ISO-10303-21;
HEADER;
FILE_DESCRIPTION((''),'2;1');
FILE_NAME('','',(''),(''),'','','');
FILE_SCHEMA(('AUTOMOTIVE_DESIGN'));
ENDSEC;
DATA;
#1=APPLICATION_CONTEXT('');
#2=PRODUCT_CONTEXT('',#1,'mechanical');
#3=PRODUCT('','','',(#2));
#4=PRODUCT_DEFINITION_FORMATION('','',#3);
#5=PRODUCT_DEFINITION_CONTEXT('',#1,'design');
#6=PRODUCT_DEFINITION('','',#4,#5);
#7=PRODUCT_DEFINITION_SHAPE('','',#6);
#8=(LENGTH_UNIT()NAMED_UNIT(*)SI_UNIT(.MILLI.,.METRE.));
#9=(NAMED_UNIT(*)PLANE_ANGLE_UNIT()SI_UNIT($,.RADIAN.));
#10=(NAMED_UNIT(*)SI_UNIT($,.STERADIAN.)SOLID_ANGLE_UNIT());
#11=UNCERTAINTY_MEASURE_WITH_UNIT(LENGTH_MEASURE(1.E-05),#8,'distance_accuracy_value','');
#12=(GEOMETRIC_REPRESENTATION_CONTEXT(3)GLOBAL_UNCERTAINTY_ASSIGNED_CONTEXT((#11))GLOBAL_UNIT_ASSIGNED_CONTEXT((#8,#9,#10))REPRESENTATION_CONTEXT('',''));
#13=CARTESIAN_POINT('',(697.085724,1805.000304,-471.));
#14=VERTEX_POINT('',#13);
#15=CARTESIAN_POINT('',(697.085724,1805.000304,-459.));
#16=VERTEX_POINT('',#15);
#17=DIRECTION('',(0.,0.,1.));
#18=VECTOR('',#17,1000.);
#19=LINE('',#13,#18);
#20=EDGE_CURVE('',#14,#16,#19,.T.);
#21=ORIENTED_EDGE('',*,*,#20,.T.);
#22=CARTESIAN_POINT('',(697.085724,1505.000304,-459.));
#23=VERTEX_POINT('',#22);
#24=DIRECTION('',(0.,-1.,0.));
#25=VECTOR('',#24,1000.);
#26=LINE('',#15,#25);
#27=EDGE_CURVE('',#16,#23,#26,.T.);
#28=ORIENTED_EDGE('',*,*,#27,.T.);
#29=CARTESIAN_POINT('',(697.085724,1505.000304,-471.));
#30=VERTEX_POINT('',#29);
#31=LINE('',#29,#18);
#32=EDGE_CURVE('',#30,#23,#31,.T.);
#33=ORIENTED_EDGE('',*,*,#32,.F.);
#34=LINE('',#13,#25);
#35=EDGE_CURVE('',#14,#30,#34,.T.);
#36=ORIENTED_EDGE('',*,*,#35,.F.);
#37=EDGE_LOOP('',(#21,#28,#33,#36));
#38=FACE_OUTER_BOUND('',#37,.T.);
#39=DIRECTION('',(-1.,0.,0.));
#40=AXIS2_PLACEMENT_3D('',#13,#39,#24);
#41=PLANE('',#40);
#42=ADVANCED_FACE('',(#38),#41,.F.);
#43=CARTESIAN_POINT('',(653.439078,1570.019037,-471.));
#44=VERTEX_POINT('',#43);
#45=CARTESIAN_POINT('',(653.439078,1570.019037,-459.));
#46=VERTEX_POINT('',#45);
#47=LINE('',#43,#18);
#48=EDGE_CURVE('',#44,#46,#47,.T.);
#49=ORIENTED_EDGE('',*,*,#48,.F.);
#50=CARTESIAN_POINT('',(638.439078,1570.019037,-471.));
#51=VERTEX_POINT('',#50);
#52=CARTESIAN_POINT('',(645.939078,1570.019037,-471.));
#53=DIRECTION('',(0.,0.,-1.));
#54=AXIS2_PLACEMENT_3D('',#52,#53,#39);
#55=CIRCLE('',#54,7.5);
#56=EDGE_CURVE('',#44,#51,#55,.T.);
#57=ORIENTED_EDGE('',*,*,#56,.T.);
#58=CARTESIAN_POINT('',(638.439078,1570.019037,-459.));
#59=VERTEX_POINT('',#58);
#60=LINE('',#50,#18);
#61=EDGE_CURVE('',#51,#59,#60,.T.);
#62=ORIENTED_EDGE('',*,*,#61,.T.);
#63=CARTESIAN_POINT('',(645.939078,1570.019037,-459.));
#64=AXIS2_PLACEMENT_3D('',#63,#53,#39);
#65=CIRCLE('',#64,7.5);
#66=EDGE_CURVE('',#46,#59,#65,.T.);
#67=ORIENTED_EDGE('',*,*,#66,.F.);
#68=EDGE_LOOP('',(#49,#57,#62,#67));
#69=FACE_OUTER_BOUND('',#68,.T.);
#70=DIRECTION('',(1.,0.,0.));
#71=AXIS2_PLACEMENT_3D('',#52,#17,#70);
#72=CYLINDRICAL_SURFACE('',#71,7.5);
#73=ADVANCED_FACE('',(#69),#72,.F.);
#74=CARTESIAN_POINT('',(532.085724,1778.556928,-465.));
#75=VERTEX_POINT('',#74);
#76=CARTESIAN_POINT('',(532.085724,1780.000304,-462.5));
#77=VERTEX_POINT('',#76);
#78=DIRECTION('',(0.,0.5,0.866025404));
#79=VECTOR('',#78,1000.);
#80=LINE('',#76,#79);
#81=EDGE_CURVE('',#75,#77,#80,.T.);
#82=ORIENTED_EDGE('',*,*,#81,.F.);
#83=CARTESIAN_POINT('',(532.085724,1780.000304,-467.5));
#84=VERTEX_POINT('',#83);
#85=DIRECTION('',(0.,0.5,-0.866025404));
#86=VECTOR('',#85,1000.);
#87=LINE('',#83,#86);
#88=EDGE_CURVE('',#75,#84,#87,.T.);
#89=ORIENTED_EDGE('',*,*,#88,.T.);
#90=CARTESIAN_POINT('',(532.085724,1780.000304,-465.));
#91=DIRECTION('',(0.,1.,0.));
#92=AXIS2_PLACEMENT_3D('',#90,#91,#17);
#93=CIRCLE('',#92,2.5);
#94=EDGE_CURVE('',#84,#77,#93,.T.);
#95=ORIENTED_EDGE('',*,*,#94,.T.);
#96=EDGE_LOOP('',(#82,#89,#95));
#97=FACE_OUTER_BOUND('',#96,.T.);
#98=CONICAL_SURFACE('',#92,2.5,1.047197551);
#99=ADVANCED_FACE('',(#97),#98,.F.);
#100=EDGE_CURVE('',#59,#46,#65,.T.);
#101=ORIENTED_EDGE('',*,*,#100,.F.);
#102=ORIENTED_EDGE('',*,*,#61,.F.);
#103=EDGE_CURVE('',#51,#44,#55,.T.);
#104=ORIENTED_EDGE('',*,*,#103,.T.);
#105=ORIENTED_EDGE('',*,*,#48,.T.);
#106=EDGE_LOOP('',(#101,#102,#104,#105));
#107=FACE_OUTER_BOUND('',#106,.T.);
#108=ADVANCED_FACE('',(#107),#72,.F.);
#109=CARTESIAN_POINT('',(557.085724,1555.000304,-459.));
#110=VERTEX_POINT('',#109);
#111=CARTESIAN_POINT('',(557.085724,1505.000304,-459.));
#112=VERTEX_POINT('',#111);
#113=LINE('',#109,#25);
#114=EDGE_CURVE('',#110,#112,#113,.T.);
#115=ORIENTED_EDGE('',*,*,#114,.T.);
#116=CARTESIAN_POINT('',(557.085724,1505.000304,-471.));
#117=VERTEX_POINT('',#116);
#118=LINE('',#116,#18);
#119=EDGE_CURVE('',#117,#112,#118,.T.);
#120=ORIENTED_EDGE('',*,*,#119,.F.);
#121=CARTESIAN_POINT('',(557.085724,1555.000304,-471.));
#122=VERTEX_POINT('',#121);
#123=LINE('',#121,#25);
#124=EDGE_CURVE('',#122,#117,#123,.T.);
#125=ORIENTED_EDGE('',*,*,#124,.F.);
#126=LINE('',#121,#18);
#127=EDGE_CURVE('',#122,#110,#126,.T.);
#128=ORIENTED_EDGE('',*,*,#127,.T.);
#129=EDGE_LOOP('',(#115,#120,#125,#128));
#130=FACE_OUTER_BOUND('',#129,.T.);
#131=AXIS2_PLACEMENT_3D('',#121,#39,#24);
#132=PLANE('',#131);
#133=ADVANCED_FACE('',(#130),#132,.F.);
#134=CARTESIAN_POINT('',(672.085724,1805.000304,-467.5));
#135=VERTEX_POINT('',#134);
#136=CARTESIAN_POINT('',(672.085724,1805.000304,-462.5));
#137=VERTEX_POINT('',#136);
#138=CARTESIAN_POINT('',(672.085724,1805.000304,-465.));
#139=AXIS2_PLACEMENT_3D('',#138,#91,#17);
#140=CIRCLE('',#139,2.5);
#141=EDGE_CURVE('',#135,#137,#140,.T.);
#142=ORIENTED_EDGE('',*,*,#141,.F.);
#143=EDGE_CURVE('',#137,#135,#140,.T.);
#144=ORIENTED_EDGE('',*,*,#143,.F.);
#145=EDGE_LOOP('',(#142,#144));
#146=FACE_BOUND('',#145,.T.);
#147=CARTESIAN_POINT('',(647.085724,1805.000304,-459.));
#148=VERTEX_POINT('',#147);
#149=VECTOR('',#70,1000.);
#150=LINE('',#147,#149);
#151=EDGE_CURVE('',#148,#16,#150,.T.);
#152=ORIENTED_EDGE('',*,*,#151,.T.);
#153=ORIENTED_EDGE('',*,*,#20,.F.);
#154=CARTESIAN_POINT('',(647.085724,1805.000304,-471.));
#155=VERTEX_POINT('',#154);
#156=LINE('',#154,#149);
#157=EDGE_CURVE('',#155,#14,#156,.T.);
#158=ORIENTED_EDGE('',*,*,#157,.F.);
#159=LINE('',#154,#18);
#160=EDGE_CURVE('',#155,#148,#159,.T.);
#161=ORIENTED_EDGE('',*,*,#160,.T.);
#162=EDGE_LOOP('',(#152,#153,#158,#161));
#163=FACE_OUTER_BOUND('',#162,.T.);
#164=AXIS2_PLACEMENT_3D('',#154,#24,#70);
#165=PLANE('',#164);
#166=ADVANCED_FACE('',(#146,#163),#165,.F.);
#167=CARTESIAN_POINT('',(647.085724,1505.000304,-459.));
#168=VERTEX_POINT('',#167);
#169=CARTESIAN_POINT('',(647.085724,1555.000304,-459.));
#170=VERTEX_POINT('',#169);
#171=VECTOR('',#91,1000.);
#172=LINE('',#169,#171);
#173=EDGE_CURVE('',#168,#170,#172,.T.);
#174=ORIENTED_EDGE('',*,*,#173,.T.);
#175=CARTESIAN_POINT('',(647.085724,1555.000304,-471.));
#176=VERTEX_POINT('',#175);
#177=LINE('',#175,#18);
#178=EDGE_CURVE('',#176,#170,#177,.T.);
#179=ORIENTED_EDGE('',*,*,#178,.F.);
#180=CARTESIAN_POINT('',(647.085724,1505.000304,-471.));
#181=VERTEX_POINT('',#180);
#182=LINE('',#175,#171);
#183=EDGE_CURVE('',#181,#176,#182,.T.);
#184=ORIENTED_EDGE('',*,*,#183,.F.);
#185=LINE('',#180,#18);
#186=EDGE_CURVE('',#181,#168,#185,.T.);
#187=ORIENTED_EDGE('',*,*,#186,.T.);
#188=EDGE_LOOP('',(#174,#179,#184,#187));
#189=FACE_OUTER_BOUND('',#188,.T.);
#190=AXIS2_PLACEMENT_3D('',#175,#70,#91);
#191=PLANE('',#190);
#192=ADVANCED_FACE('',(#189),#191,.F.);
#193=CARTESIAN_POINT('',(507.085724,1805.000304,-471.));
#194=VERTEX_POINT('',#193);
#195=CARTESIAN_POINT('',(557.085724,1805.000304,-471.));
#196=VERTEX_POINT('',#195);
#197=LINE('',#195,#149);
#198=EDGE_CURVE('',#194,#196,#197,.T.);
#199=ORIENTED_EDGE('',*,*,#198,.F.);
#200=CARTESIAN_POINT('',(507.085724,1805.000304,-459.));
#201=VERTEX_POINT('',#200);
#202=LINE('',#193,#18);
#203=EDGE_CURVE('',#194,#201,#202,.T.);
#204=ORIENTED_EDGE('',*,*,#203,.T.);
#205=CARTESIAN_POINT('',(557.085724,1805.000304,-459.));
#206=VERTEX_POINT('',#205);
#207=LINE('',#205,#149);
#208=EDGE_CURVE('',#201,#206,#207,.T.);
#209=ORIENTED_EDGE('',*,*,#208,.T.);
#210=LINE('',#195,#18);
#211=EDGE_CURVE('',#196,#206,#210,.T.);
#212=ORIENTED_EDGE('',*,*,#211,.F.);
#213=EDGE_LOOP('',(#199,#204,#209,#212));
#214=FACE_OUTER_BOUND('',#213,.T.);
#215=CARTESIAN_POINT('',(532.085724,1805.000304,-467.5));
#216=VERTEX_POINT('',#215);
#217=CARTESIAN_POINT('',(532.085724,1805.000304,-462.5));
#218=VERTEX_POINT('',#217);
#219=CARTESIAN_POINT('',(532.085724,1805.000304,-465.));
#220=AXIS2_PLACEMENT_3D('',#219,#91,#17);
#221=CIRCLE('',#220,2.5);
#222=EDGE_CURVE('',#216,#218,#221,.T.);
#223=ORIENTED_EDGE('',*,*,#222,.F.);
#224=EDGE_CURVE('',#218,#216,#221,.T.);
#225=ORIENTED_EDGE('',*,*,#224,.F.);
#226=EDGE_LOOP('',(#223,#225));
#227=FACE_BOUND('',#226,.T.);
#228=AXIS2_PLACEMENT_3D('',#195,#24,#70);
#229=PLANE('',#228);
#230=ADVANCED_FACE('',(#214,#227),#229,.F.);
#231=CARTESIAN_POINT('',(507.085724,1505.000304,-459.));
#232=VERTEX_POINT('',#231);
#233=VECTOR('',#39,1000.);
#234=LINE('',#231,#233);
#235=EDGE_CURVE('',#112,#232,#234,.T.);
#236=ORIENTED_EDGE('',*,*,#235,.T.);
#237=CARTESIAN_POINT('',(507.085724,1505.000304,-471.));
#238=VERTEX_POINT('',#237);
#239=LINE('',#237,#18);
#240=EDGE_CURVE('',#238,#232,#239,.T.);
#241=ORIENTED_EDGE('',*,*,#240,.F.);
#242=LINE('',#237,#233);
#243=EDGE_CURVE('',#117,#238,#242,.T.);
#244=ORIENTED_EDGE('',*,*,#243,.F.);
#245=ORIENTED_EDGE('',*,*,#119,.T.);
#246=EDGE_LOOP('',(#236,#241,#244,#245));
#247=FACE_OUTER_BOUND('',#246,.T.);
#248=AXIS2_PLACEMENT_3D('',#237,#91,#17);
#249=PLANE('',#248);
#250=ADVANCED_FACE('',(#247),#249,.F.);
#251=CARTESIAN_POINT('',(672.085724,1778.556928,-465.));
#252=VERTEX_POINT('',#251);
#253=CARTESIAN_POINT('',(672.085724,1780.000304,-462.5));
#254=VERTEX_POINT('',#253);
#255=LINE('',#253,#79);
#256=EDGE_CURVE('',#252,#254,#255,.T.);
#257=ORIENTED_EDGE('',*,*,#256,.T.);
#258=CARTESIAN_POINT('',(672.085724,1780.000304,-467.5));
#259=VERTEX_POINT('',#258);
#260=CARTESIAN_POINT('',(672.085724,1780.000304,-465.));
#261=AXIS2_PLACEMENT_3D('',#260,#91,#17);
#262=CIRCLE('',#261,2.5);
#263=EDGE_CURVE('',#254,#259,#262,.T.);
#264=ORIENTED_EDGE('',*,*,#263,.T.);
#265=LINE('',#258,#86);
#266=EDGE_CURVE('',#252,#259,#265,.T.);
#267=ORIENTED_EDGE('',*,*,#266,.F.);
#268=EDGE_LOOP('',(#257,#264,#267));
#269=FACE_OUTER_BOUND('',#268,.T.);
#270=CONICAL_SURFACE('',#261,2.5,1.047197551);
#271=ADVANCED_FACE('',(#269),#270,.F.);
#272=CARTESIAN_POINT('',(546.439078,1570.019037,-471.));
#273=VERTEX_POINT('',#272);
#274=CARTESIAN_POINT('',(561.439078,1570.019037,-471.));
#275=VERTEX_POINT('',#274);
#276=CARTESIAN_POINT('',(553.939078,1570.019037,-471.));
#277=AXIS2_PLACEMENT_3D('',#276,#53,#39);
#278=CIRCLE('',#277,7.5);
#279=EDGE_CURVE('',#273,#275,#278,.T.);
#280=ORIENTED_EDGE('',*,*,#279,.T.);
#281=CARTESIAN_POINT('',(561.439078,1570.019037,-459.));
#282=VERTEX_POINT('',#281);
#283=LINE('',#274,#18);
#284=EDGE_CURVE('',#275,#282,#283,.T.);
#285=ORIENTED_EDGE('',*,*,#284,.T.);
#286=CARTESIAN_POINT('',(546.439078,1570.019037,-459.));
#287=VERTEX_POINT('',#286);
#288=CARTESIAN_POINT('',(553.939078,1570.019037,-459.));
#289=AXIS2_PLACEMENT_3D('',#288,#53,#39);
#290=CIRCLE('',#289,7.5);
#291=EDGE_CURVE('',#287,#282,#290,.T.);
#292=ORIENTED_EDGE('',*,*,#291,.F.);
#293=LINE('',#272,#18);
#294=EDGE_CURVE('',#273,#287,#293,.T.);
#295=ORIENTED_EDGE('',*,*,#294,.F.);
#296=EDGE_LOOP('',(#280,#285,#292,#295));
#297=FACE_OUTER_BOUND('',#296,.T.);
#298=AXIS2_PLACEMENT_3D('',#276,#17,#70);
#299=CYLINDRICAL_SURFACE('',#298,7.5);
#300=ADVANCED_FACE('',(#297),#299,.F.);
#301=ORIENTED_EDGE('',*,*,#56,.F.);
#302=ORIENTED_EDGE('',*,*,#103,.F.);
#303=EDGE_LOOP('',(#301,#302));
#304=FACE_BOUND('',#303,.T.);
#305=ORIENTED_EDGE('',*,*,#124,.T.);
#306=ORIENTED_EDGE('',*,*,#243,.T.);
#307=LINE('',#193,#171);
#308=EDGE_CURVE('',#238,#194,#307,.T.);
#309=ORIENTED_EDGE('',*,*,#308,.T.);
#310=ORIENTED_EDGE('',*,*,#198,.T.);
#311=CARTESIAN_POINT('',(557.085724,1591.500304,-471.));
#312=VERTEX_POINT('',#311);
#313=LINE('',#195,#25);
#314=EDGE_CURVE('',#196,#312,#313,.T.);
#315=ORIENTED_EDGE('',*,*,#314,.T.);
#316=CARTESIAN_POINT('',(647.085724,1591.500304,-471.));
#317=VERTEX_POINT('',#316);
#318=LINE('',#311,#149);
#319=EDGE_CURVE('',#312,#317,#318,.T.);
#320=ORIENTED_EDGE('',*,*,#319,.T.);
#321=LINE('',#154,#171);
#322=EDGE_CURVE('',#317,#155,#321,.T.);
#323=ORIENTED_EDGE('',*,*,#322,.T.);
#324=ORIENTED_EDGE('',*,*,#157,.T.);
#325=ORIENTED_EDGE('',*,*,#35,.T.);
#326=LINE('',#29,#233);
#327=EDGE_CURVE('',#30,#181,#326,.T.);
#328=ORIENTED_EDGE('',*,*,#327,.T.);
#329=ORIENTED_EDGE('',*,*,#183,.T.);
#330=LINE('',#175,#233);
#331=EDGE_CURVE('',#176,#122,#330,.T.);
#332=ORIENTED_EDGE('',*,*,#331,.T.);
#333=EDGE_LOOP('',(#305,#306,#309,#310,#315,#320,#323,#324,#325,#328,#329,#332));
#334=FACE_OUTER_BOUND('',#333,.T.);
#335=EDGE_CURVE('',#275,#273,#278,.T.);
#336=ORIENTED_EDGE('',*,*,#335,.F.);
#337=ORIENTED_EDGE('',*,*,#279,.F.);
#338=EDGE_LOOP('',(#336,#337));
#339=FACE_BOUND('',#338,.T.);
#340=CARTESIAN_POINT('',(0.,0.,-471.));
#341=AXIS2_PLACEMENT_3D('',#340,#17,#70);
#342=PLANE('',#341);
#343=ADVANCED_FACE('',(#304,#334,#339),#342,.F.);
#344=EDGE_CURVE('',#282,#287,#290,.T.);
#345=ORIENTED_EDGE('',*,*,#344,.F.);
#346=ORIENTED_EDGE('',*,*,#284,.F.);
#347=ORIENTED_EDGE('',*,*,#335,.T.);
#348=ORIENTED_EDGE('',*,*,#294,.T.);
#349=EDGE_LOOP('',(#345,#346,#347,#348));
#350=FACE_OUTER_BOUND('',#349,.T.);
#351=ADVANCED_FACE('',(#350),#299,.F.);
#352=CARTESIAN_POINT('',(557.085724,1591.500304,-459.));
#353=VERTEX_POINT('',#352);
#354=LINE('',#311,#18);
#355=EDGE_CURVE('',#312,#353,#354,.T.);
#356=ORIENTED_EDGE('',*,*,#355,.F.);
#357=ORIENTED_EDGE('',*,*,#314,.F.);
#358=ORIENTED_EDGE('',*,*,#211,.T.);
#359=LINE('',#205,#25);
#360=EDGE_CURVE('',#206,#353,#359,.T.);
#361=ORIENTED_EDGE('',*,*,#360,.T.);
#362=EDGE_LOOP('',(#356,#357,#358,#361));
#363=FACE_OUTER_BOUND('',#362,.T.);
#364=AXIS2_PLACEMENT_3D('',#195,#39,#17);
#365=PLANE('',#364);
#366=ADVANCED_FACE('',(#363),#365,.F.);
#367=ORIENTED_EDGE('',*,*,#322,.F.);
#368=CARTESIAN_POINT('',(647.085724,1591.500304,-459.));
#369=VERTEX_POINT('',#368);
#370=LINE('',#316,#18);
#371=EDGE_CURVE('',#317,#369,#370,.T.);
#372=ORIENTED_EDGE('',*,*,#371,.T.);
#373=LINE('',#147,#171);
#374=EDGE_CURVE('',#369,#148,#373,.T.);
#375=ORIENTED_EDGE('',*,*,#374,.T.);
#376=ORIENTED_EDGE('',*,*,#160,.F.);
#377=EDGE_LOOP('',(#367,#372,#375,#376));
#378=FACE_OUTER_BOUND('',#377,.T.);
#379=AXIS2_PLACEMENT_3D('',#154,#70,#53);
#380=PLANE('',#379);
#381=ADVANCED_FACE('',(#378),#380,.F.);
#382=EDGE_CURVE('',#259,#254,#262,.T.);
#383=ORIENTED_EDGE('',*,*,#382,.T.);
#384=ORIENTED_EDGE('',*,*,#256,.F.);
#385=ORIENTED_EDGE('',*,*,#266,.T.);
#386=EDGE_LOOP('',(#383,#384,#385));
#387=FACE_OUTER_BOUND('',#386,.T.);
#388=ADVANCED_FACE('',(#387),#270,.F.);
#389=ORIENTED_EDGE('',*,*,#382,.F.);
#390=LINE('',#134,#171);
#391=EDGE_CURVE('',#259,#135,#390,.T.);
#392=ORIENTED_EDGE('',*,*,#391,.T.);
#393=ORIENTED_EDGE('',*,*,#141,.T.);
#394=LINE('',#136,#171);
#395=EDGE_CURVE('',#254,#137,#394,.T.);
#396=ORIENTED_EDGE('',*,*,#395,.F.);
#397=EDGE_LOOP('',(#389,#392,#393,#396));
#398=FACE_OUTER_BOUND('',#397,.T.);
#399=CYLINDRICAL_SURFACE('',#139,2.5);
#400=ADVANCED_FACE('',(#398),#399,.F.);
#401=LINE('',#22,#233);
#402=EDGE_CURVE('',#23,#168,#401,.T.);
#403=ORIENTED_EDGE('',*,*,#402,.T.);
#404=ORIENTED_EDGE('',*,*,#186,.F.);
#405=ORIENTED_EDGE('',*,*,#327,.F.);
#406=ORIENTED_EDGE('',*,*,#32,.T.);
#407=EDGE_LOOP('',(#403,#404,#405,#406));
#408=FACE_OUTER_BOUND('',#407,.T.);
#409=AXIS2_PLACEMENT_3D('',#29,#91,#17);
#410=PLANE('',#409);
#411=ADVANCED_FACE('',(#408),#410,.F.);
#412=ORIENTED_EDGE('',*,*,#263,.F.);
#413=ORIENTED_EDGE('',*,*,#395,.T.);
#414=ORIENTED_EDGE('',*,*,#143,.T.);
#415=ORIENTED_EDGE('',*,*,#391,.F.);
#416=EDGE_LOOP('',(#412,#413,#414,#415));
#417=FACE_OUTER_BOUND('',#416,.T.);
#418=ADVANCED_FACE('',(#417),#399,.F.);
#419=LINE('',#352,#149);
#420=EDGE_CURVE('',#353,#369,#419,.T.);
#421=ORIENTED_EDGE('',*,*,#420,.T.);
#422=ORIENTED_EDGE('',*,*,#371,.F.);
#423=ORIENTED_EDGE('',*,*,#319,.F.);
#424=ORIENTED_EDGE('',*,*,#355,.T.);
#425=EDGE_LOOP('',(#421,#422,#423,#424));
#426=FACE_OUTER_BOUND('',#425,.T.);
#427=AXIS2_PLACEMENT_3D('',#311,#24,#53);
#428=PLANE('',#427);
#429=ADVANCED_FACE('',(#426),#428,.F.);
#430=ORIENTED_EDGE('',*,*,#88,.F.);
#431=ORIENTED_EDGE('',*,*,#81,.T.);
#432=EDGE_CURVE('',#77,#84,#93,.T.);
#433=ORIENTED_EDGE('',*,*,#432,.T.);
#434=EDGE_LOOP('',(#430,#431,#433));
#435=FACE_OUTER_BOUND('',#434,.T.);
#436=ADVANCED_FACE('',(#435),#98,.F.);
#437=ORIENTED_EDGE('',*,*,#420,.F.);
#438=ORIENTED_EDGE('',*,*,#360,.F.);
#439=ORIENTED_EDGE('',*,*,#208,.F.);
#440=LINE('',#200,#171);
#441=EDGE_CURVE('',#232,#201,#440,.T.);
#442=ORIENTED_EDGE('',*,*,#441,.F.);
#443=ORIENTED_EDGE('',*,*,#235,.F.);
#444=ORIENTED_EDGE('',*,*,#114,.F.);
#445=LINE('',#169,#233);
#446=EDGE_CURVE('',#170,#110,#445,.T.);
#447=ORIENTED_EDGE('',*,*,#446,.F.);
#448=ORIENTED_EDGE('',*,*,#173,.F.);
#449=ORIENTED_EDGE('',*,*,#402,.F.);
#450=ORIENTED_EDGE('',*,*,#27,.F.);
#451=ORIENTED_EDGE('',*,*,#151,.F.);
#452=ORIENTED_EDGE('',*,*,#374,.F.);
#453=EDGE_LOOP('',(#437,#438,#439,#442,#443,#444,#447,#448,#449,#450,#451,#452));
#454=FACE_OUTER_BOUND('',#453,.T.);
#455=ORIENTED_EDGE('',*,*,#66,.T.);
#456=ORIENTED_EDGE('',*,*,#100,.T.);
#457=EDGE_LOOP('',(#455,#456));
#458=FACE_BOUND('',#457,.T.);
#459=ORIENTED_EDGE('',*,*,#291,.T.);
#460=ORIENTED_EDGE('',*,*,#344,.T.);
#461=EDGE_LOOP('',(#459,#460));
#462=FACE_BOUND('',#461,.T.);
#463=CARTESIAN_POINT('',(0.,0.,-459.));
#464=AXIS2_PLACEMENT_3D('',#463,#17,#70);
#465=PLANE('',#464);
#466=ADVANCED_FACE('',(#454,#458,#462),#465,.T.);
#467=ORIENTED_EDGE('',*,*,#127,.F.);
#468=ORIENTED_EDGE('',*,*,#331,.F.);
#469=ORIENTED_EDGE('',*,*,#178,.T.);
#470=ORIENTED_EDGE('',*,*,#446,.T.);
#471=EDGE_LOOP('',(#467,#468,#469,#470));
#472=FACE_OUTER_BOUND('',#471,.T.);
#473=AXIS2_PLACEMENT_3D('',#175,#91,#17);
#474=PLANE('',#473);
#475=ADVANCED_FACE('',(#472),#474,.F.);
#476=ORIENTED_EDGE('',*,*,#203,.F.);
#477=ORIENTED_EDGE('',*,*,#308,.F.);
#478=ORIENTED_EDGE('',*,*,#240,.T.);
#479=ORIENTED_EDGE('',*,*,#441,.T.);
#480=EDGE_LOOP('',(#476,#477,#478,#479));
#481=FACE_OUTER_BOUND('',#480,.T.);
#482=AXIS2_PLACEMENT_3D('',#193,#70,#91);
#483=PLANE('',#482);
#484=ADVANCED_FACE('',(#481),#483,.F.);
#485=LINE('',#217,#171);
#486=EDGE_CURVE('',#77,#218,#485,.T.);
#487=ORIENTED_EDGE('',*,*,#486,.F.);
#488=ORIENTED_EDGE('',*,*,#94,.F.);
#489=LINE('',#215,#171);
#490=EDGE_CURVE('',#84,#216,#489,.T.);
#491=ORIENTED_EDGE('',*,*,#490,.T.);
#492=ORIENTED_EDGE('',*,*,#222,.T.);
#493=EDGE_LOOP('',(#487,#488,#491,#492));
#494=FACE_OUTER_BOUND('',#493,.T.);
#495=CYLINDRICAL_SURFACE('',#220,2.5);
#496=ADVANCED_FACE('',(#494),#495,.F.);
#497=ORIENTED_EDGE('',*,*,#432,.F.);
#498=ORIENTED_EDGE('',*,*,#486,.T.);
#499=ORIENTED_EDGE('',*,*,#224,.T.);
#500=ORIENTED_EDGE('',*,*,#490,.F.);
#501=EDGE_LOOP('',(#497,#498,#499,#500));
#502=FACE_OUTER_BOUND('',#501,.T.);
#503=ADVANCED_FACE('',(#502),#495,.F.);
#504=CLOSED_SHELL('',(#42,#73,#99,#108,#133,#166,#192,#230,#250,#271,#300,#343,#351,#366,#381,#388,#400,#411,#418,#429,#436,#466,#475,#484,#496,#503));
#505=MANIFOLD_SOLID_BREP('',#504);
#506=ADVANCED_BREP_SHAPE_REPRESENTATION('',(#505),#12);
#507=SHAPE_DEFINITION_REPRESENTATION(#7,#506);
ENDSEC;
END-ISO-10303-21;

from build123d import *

# Parameters (mm, degrees)
SKETCH_1_R             = 7.5
EXTRUDE_1_DEPTH        = 6
HOLE_WIZARD_M6_1_D     = 5
HOLE_WIZARD_M6_1_DEPTH = 25
HOLE_WIZARD_M6_1_TIP   = 1.443375673


with BuildPart() as part:
    # 草图1 → 凸台-拉伸1 (new, symmetric)
    with BuildSketch(Plane(origin=(0, 0, -465), x_dir=(-1, 0, 0), z_dir=(0, 0, -1))):
        Polygon((-557.085724054, 1805.000303929), (-557.085724054, 1591.500303929), (-647.085724054, 1591.500303929), (-647.085724054, 1805.000303929), (-697.085724054, 1805.000303929), (-697.085724054, 1505.000303929), (-647.085724054, 1505.000303929), (-647.085724054, 1555.000303929), (-557.085724054, 1555.000303929), (-557.085724054, 1505.000303929), (-507.085724054, 1505.000303929), (-507.085724054, 1805.000303929), align=None)
        with Locations((-553.939078063, 1570.019037425)):
            Circle(SKETCH_1_R, mode=Mode.SUBTRACT)
        with Locations((-645.939078063, 1570.019037425)):
            Circle(SKETCH_1_R, mode=Mode.SUBTRACT)
    extrude(amount=EXTRUDE_1_DEPTH, both=True)

    # M6 螺纹孔1
    with Locations(Plane(origin=(0, 1805.000303929, 0), x_dir=(1, 0, 0), z_dir=(0, 1, 0))):
        with Locations((672.085724054, 465), (532.085724054, 465)):
            Hole(HOLE_WIZARD_M6_1_D / 2, depth=HOLE_WIZARD_M6_1_DEPTH)
            with Locations((0, 0, -(HOLE_WIZARD_M6_1_DEPTH + HOLE_WIZARD_M6_1_TIP / 2))):  # 120° drill point
                Cone(0, HOLE_WIZARD_M6_1_D / 2, HOLE_WIZARD_M6_1_TIP, mode=Mode.SUBTRACT)


solid = part.part
